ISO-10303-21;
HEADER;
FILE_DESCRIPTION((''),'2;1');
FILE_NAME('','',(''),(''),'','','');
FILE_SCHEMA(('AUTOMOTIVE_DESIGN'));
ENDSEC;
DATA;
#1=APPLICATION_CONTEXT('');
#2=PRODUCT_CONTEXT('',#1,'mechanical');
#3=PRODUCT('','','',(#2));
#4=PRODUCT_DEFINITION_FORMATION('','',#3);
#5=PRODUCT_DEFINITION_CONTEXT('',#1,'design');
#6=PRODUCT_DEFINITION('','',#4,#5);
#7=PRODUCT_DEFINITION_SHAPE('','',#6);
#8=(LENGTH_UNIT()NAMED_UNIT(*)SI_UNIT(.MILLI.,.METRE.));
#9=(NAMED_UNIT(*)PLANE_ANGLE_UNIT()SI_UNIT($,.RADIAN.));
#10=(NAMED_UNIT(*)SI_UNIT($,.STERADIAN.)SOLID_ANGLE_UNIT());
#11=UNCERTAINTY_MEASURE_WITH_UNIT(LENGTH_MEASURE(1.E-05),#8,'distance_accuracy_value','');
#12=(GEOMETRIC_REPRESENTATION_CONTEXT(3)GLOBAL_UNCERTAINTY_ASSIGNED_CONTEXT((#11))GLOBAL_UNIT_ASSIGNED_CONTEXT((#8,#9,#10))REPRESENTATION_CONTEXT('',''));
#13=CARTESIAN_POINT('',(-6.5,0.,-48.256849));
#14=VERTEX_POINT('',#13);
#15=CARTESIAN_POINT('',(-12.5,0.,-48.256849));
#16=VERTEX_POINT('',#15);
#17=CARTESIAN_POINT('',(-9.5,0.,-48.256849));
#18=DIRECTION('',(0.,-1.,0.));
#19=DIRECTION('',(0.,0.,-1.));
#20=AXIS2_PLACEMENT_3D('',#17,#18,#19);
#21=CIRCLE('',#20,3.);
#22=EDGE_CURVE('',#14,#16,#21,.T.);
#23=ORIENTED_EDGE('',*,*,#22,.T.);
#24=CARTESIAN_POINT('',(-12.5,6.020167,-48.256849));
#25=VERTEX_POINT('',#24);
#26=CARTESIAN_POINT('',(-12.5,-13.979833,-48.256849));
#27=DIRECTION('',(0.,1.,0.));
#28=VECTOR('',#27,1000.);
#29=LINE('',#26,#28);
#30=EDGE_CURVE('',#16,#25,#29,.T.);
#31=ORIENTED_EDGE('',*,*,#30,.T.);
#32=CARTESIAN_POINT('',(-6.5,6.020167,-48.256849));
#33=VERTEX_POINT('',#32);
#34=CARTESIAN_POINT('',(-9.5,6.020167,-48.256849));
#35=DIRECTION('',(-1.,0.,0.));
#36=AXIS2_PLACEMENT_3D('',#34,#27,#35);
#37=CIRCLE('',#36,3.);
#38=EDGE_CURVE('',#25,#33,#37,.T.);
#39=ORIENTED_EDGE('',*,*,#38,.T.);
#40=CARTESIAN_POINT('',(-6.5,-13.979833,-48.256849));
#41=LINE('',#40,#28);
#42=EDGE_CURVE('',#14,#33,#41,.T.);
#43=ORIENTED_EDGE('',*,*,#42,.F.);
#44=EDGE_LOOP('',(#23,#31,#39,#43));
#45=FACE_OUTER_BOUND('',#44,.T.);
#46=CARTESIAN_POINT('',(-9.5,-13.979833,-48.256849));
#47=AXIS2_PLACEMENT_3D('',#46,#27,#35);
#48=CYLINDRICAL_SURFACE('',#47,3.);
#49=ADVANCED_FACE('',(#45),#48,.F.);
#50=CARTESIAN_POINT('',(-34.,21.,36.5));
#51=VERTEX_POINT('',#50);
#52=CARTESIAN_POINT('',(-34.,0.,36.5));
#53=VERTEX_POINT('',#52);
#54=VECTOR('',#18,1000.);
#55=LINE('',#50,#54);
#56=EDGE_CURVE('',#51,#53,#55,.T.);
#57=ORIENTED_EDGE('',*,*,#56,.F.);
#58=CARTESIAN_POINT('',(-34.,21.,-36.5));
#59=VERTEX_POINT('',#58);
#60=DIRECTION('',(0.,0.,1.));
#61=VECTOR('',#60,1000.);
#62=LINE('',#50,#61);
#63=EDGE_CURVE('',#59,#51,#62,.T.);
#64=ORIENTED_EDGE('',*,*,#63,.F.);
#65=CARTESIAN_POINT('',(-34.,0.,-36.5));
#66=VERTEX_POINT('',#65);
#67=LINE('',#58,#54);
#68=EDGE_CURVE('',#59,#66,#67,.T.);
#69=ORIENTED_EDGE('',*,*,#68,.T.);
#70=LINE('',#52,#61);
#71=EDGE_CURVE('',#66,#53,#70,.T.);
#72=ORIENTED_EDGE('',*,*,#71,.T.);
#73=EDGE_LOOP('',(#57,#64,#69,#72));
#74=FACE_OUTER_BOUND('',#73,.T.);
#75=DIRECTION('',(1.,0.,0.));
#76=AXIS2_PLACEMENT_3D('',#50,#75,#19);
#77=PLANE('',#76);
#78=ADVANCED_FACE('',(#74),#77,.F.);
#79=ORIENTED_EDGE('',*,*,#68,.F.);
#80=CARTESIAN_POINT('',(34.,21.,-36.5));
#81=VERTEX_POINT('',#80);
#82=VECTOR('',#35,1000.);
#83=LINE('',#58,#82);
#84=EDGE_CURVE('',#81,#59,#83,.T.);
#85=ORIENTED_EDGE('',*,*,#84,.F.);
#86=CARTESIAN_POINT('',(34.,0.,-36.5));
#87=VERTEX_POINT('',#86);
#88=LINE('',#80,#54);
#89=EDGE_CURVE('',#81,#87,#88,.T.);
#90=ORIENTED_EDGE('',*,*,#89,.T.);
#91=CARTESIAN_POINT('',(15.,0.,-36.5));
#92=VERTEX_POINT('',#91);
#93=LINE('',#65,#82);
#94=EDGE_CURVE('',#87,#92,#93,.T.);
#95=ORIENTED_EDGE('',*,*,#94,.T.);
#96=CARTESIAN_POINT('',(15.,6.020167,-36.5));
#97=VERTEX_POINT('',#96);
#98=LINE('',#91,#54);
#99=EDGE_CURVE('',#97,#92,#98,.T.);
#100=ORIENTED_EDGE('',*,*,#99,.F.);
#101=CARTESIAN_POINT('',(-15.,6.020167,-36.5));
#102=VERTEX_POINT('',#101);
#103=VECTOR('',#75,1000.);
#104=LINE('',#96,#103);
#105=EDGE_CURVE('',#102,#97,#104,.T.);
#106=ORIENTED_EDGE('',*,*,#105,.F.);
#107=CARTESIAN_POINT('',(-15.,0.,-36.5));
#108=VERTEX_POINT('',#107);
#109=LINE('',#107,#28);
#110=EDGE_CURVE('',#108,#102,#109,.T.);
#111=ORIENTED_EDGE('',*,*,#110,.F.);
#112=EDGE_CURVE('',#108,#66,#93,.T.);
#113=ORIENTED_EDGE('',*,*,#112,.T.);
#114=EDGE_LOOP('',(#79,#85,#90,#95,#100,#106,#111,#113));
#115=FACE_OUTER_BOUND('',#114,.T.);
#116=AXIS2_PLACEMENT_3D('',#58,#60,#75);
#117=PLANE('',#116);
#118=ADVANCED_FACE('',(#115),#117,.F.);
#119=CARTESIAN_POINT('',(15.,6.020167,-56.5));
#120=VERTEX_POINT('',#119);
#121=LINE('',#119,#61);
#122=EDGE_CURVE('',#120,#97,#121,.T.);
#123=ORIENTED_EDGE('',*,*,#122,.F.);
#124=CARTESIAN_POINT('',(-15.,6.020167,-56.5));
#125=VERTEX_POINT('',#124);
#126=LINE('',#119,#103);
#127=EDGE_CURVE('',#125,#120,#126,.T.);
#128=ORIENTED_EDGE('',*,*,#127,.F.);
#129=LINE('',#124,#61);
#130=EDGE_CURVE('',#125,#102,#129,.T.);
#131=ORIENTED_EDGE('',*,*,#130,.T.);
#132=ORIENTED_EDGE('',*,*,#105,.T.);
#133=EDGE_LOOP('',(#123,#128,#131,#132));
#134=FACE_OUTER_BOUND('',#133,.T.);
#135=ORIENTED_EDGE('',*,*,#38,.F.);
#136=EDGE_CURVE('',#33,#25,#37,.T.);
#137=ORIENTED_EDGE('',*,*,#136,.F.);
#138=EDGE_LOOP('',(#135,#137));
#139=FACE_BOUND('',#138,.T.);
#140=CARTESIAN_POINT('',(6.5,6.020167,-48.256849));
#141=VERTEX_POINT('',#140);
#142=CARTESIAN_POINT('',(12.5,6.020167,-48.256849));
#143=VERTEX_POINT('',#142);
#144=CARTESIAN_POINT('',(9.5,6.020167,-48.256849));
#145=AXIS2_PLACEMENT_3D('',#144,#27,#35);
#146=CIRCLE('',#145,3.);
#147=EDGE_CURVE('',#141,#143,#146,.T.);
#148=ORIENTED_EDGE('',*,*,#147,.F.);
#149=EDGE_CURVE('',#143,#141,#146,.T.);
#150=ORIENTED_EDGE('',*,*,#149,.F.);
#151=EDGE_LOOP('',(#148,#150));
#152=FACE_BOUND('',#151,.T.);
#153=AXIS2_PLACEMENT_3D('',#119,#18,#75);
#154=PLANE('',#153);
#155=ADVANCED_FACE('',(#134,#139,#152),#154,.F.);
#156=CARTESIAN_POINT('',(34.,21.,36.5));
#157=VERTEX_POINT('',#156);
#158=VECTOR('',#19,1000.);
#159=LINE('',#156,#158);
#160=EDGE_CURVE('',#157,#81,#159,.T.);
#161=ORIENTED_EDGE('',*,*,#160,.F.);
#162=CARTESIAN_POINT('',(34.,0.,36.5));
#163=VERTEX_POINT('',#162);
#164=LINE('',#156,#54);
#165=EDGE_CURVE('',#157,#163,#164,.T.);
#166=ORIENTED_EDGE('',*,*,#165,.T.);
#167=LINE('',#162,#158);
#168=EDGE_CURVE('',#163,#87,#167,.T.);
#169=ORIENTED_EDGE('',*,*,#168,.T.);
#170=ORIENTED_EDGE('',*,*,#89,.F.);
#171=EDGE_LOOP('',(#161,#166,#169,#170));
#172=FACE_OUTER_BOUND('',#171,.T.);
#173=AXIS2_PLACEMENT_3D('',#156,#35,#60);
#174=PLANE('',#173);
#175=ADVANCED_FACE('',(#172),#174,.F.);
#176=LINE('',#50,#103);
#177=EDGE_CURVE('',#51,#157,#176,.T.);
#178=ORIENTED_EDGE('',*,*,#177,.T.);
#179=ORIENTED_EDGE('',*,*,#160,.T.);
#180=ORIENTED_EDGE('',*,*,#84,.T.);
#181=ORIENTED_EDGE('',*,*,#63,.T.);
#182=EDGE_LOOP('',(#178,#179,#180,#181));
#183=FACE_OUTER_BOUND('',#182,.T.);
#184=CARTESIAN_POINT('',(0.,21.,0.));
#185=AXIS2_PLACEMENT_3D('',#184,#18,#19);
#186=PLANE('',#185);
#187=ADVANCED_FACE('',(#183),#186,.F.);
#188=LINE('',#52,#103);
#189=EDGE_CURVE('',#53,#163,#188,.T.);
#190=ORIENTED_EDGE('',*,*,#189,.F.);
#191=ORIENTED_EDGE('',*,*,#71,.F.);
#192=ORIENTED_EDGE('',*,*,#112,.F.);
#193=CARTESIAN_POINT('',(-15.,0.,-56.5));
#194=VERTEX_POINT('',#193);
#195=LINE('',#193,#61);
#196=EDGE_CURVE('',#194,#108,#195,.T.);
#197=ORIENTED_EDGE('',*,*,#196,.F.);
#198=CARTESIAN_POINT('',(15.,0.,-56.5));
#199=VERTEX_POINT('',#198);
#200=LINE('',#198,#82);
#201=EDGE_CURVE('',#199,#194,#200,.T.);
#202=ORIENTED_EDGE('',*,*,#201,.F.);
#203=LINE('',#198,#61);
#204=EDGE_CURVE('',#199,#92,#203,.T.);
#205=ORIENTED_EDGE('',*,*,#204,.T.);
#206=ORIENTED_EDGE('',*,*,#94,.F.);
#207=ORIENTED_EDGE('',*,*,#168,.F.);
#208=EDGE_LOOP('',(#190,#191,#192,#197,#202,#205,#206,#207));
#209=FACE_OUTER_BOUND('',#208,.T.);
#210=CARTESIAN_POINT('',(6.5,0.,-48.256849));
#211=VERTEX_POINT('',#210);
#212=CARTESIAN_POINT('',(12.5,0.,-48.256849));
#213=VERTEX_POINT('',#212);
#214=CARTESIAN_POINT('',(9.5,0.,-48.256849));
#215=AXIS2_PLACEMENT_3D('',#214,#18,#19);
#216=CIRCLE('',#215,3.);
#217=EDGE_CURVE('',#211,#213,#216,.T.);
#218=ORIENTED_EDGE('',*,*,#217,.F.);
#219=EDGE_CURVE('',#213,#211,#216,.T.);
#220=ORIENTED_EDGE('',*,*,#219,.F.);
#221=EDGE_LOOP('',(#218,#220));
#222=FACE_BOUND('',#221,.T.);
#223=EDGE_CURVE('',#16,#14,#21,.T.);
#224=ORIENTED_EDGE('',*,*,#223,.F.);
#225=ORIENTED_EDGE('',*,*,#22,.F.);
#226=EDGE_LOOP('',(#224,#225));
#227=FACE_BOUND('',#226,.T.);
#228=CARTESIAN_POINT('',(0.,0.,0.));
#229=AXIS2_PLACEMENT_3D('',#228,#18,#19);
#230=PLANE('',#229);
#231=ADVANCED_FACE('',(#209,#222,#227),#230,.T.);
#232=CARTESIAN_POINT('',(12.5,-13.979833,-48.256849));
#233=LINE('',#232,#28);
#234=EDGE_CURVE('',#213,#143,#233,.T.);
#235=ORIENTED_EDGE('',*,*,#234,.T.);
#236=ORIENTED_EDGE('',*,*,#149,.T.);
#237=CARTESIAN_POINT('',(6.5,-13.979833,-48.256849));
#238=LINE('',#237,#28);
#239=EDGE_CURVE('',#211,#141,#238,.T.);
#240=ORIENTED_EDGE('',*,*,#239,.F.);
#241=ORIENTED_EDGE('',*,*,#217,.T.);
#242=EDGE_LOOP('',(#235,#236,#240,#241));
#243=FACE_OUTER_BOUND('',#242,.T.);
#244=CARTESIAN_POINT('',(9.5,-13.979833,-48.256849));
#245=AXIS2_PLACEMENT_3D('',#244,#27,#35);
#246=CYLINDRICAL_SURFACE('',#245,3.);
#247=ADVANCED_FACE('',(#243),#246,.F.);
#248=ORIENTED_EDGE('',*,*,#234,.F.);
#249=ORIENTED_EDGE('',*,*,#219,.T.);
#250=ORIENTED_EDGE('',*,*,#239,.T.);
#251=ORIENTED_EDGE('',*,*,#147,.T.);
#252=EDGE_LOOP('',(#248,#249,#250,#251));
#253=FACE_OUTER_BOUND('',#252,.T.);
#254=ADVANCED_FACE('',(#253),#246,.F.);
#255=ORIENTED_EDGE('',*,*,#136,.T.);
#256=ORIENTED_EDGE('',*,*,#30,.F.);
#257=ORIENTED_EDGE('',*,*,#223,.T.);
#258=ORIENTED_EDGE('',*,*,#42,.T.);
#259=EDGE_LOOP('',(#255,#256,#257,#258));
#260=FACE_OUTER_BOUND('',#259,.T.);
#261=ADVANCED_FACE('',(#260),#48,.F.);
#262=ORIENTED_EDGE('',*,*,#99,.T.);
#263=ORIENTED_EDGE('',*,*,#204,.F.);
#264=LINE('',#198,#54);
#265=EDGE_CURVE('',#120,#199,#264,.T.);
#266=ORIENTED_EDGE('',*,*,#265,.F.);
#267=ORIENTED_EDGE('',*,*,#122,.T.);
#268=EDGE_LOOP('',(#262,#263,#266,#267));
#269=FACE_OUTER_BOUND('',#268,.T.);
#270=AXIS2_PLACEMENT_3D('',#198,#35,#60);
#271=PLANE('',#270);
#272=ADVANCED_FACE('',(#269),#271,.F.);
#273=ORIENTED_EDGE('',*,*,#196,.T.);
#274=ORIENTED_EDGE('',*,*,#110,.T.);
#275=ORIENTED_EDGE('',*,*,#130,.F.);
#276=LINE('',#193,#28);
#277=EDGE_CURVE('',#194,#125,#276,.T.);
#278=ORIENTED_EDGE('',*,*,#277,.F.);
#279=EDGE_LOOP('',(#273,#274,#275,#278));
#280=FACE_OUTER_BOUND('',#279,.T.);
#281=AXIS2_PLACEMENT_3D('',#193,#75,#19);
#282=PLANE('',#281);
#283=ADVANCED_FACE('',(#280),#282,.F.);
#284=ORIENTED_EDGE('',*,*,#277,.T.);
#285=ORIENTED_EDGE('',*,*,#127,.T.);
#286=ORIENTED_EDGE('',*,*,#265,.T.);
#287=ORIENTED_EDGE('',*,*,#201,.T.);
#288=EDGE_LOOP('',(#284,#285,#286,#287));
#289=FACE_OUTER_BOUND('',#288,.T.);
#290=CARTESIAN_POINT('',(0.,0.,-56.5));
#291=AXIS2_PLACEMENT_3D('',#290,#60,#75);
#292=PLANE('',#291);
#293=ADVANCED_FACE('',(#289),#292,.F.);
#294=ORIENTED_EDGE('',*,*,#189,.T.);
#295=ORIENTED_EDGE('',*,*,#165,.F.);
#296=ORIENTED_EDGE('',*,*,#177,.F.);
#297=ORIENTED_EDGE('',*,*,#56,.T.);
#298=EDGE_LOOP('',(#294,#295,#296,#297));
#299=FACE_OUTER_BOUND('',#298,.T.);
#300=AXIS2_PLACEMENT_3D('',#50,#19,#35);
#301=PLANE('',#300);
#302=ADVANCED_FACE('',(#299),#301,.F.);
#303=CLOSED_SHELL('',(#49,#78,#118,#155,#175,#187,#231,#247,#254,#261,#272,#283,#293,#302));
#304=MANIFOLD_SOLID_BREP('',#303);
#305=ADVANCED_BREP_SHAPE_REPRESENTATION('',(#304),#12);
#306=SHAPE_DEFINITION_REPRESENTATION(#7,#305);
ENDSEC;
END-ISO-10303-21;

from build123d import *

# Parameters (mm, degrees)
SKETCH1_W           = 68
SKETCH1_H           = 73
BOSS_EXTRUDE1_DEPTH = 21
SKETCH2_W           = 30
SKETCH2_H           = 6.020166846
BOSS_EXTRUDE2_DEPTH = 20
SKETCH3_R           = 3
CUT_EXTRUDE1_DEPTH  = 20


with BuildPart() as part:
    # Sketch1 → Boss-Extrude1 (new body)
    with BuildSketch(Plane(origin=(0, 0, 0), x_dir=(1, 0, 0), z_dir=(0, 1, 0))):
        Rectangle(SKETCH1_W, SKETCH1_H)
    extrude(amount=BOSS_EXTRUDE1_DEPTH)

    # Sketch2 → Boss-Extrude2 (add)
    with BuildSketch(Plane(origin=(0, 0, -36.5), x_dir=(-1, 0, 0), z_dir=(0, 0, -1))):
        with Locations((0, 3.010083423)):
            Rectangle(SKETCH2_W, SKETCH2_H)
    extrude(amount=BOSS_EXTRUDE2_DEPTH)

    # Sketch3 → Cut-Extrude1 (cut)
    with BuildSketch(Plane(origin=(0, 6.020166846, 0), x_dir=(1, 0, 0), z_dir=(0, 1, 0))):
        with Locations(Location((9.5, 48.256848867, 0), (0, 0, 180))):
            Circle(SKETCH3_R)
        with Locations(Location((-9.5, 48.256848867, 0), (0, 0, 180))):
            Circle(SKETCH3_R)
    extrude(amount=-CUT_EXTRUDE1_DEPTH, mode=Mode.SUBTRACT)


solid = part.part
